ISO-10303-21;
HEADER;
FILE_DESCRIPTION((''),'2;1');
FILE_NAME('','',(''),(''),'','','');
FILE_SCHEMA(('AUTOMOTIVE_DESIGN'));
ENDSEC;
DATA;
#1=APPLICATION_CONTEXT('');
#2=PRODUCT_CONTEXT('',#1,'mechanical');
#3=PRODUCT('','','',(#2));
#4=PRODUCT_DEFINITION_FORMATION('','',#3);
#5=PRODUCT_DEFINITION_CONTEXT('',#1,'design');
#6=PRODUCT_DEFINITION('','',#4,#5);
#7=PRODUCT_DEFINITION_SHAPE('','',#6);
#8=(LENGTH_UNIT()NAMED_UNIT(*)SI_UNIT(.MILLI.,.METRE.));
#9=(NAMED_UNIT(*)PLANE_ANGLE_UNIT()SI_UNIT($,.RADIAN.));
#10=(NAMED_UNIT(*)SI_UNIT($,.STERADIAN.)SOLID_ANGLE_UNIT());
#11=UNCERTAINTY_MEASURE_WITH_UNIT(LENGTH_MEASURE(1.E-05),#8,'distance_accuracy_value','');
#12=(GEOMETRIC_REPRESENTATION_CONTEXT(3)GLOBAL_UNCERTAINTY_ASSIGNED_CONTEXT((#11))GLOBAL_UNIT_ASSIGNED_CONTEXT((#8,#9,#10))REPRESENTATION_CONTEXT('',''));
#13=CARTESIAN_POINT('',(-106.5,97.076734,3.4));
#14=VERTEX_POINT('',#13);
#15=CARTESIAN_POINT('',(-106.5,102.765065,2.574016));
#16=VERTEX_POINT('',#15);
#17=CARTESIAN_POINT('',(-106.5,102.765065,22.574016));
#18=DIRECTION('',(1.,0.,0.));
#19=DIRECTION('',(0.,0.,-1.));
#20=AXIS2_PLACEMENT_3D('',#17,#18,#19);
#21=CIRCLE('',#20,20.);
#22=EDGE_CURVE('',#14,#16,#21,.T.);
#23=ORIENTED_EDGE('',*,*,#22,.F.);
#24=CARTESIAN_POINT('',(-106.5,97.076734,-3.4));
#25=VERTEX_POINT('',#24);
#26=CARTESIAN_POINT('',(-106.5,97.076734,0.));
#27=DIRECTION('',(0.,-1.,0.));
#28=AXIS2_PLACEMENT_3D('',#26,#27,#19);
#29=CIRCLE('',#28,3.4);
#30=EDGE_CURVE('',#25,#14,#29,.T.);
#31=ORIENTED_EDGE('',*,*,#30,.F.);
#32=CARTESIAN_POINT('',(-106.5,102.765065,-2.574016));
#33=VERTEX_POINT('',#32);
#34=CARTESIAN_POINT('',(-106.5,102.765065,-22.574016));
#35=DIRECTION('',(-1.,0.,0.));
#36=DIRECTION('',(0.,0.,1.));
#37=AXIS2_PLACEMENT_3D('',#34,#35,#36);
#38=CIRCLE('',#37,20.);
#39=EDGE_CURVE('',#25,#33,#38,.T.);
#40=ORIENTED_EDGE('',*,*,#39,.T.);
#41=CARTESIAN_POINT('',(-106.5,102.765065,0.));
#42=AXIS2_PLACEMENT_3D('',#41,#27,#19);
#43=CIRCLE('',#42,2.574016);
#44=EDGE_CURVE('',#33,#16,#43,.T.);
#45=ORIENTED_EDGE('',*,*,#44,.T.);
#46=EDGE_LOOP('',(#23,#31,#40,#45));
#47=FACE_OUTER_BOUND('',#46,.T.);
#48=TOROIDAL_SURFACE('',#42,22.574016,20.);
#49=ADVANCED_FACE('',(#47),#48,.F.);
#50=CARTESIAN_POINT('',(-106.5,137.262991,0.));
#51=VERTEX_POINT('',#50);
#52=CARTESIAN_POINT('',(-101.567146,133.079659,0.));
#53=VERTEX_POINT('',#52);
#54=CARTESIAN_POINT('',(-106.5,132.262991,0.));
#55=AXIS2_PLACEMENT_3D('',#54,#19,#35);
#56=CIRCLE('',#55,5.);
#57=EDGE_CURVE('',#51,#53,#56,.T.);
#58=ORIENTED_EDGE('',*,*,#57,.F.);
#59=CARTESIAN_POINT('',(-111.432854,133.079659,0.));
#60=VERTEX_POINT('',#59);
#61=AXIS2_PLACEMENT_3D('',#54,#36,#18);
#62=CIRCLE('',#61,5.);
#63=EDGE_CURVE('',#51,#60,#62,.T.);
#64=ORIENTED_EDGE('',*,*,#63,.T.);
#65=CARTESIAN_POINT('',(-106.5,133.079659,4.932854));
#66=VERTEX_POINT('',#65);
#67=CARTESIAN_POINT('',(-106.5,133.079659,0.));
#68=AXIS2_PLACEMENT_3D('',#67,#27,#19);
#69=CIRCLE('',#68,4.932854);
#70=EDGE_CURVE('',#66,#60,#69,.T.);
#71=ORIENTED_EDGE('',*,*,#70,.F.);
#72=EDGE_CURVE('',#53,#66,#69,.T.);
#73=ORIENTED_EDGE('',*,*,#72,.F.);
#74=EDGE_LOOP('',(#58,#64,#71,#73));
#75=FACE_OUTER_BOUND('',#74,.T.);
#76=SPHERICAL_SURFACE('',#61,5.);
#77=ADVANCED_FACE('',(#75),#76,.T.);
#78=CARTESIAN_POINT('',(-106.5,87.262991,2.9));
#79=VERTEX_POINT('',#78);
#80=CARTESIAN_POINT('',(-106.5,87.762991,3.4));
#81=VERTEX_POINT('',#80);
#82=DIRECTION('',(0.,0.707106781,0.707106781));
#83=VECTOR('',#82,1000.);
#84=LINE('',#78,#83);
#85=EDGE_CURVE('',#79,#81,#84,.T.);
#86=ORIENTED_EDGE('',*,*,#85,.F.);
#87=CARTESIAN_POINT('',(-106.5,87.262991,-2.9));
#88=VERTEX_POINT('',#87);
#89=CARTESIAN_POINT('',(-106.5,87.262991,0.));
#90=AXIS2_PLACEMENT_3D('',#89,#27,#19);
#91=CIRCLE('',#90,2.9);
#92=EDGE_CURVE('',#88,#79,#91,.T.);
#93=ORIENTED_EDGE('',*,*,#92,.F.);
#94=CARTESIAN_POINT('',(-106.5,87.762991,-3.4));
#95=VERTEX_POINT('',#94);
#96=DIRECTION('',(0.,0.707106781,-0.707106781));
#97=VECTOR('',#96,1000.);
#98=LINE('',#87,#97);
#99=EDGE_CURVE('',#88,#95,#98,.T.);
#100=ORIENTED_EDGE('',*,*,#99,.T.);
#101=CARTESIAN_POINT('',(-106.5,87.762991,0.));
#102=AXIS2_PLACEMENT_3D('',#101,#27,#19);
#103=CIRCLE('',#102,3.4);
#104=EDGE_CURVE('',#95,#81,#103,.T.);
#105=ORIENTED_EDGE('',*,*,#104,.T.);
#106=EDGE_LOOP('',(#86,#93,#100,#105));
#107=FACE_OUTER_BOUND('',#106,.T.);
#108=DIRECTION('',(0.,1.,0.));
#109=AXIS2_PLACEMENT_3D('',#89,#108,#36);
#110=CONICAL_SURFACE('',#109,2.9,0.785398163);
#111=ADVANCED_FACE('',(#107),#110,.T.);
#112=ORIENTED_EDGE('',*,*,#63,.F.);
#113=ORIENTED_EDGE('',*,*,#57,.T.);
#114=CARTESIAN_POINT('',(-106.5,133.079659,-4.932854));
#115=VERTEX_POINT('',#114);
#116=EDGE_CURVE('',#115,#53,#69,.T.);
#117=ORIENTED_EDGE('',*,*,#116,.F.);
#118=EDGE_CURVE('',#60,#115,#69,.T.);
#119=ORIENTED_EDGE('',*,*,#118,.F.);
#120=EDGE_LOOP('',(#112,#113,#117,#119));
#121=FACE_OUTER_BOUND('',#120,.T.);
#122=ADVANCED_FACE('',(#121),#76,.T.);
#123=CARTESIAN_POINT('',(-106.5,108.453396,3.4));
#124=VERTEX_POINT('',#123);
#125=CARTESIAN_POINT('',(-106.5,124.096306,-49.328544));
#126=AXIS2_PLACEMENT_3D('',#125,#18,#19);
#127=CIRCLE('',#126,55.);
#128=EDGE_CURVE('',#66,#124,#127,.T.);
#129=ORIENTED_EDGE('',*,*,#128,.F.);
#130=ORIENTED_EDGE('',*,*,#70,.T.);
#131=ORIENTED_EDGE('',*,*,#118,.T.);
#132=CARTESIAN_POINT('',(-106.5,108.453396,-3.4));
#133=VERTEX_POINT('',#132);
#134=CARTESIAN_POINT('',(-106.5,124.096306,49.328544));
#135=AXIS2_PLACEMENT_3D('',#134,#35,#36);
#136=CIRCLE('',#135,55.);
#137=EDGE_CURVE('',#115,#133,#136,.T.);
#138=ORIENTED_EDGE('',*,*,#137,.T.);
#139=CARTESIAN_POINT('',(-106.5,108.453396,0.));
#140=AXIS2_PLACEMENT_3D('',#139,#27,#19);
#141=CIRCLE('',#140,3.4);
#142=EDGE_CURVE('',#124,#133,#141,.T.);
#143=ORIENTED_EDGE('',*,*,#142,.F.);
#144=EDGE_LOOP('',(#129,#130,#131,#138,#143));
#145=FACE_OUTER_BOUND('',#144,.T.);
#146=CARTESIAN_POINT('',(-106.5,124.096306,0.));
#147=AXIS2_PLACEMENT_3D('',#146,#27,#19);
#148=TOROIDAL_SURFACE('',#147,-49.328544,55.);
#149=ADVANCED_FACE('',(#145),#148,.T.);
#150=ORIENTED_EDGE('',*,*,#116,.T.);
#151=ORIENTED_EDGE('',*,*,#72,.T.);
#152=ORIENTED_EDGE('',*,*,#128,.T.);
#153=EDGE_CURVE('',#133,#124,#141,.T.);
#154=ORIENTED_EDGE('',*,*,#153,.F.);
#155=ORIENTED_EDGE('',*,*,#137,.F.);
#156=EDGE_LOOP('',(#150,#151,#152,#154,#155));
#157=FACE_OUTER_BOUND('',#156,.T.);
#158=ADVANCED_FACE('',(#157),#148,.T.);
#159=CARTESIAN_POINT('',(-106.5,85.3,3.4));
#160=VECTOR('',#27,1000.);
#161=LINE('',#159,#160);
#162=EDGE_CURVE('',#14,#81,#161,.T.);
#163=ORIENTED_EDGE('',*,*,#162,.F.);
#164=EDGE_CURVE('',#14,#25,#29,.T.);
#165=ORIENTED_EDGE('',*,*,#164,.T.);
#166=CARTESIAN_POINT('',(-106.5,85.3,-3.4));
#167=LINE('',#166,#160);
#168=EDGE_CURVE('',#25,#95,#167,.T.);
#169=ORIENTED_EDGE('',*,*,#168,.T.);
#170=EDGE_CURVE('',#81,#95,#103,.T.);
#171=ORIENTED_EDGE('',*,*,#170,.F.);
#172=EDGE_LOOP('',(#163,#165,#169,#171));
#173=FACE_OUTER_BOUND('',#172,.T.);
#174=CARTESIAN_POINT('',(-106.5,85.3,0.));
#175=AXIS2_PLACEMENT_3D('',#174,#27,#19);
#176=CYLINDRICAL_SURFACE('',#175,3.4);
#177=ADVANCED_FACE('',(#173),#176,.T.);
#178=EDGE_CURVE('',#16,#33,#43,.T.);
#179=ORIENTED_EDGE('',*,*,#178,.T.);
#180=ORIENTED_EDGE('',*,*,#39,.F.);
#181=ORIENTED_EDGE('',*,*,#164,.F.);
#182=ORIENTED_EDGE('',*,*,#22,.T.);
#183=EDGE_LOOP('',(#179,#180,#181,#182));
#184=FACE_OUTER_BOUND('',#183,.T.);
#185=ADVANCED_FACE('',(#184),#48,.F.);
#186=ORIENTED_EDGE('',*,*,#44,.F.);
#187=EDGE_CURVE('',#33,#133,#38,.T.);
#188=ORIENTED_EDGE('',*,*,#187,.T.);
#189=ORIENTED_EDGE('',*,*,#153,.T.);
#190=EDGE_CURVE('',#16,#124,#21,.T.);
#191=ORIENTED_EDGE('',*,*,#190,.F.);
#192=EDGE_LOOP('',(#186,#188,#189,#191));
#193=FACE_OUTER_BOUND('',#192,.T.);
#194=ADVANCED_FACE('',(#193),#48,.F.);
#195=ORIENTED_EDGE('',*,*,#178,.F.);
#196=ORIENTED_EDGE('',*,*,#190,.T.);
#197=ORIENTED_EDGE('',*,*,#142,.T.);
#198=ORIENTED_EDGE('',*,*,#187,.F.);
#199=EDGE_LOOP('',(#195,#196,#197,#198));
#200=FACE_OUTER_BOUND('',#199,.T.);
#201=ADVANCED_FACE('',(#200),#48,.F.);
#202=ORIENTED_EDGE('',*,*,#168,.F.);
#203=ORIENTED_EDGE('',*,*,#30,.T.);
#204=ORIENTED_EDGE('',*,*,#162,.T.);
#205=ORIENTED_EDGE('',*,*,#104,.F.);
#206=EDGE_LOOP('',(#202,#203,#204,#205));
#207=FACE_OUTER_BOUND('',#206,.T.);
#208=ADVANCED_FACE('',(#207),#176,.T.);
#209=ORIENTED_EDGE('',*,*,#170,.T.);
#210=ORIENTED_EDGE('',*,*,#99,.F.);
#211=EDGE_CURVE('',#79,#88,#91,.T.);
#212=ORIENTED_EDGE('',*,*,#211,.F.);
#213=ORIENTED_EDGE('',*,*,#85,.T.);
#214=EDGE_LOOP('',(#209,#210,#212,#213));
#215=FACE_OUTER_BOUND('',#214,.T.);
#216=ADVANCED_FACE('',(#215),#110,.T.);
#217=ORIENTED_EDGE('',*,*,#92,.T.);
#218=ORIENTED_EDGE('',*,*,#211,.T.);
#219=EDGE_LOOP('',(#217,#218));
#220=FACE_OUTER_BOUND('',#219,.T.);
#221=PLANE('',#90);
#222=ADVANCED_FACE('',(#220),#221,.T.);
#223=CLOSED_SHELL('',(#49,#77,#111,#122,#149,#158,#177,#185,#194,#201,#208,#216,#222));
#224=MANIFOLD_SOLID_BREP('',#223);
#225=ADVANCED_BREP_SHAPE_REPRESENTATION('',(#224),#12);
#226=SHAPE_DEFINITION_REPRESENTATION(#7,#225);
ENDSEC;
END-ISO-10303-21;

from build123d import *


with BuildPart() as part:
    # Sketch1 → Revolve1 (revolve)
    with BuildSketch(Plane.XY, mode=Mode.PRIVATE) as revolve1_sk:
        with BuildLine():
            Line((-103.1, 87.762990915), (-103.1, 97.076733695))
            ThreePointArc((-103.1, 97.076733695), (-103.925983982, 102.765064712), (-103.1, 108.453395729))
            ThreePointArc((-103.1, 108.453395729), (-100.934781518, 120.679460223), (-101.567145595, 133.079659404))
            ThreePointArc((-101.567145595, 133.079659404), (-103.266066052, 136.076345242), (-106.5, 137.262990915))
            Line((-106.5, 137.262990915), (-106.5, 87.262990915))
            Line((-106.5, 87.262990915), (-103.6, 87.262990915))
            Line((-103.6, 87.262990915), (-103.1, 87.762990915))
        make_face()
    revolve(revolve1_sk.sketch.rotate(Axis((-106.5, 85.3, 0), (0, 1, 0)), 90), axis=Axis((-106.5, 85.3, 0), (0, 1, 0)))


solid = part.part
